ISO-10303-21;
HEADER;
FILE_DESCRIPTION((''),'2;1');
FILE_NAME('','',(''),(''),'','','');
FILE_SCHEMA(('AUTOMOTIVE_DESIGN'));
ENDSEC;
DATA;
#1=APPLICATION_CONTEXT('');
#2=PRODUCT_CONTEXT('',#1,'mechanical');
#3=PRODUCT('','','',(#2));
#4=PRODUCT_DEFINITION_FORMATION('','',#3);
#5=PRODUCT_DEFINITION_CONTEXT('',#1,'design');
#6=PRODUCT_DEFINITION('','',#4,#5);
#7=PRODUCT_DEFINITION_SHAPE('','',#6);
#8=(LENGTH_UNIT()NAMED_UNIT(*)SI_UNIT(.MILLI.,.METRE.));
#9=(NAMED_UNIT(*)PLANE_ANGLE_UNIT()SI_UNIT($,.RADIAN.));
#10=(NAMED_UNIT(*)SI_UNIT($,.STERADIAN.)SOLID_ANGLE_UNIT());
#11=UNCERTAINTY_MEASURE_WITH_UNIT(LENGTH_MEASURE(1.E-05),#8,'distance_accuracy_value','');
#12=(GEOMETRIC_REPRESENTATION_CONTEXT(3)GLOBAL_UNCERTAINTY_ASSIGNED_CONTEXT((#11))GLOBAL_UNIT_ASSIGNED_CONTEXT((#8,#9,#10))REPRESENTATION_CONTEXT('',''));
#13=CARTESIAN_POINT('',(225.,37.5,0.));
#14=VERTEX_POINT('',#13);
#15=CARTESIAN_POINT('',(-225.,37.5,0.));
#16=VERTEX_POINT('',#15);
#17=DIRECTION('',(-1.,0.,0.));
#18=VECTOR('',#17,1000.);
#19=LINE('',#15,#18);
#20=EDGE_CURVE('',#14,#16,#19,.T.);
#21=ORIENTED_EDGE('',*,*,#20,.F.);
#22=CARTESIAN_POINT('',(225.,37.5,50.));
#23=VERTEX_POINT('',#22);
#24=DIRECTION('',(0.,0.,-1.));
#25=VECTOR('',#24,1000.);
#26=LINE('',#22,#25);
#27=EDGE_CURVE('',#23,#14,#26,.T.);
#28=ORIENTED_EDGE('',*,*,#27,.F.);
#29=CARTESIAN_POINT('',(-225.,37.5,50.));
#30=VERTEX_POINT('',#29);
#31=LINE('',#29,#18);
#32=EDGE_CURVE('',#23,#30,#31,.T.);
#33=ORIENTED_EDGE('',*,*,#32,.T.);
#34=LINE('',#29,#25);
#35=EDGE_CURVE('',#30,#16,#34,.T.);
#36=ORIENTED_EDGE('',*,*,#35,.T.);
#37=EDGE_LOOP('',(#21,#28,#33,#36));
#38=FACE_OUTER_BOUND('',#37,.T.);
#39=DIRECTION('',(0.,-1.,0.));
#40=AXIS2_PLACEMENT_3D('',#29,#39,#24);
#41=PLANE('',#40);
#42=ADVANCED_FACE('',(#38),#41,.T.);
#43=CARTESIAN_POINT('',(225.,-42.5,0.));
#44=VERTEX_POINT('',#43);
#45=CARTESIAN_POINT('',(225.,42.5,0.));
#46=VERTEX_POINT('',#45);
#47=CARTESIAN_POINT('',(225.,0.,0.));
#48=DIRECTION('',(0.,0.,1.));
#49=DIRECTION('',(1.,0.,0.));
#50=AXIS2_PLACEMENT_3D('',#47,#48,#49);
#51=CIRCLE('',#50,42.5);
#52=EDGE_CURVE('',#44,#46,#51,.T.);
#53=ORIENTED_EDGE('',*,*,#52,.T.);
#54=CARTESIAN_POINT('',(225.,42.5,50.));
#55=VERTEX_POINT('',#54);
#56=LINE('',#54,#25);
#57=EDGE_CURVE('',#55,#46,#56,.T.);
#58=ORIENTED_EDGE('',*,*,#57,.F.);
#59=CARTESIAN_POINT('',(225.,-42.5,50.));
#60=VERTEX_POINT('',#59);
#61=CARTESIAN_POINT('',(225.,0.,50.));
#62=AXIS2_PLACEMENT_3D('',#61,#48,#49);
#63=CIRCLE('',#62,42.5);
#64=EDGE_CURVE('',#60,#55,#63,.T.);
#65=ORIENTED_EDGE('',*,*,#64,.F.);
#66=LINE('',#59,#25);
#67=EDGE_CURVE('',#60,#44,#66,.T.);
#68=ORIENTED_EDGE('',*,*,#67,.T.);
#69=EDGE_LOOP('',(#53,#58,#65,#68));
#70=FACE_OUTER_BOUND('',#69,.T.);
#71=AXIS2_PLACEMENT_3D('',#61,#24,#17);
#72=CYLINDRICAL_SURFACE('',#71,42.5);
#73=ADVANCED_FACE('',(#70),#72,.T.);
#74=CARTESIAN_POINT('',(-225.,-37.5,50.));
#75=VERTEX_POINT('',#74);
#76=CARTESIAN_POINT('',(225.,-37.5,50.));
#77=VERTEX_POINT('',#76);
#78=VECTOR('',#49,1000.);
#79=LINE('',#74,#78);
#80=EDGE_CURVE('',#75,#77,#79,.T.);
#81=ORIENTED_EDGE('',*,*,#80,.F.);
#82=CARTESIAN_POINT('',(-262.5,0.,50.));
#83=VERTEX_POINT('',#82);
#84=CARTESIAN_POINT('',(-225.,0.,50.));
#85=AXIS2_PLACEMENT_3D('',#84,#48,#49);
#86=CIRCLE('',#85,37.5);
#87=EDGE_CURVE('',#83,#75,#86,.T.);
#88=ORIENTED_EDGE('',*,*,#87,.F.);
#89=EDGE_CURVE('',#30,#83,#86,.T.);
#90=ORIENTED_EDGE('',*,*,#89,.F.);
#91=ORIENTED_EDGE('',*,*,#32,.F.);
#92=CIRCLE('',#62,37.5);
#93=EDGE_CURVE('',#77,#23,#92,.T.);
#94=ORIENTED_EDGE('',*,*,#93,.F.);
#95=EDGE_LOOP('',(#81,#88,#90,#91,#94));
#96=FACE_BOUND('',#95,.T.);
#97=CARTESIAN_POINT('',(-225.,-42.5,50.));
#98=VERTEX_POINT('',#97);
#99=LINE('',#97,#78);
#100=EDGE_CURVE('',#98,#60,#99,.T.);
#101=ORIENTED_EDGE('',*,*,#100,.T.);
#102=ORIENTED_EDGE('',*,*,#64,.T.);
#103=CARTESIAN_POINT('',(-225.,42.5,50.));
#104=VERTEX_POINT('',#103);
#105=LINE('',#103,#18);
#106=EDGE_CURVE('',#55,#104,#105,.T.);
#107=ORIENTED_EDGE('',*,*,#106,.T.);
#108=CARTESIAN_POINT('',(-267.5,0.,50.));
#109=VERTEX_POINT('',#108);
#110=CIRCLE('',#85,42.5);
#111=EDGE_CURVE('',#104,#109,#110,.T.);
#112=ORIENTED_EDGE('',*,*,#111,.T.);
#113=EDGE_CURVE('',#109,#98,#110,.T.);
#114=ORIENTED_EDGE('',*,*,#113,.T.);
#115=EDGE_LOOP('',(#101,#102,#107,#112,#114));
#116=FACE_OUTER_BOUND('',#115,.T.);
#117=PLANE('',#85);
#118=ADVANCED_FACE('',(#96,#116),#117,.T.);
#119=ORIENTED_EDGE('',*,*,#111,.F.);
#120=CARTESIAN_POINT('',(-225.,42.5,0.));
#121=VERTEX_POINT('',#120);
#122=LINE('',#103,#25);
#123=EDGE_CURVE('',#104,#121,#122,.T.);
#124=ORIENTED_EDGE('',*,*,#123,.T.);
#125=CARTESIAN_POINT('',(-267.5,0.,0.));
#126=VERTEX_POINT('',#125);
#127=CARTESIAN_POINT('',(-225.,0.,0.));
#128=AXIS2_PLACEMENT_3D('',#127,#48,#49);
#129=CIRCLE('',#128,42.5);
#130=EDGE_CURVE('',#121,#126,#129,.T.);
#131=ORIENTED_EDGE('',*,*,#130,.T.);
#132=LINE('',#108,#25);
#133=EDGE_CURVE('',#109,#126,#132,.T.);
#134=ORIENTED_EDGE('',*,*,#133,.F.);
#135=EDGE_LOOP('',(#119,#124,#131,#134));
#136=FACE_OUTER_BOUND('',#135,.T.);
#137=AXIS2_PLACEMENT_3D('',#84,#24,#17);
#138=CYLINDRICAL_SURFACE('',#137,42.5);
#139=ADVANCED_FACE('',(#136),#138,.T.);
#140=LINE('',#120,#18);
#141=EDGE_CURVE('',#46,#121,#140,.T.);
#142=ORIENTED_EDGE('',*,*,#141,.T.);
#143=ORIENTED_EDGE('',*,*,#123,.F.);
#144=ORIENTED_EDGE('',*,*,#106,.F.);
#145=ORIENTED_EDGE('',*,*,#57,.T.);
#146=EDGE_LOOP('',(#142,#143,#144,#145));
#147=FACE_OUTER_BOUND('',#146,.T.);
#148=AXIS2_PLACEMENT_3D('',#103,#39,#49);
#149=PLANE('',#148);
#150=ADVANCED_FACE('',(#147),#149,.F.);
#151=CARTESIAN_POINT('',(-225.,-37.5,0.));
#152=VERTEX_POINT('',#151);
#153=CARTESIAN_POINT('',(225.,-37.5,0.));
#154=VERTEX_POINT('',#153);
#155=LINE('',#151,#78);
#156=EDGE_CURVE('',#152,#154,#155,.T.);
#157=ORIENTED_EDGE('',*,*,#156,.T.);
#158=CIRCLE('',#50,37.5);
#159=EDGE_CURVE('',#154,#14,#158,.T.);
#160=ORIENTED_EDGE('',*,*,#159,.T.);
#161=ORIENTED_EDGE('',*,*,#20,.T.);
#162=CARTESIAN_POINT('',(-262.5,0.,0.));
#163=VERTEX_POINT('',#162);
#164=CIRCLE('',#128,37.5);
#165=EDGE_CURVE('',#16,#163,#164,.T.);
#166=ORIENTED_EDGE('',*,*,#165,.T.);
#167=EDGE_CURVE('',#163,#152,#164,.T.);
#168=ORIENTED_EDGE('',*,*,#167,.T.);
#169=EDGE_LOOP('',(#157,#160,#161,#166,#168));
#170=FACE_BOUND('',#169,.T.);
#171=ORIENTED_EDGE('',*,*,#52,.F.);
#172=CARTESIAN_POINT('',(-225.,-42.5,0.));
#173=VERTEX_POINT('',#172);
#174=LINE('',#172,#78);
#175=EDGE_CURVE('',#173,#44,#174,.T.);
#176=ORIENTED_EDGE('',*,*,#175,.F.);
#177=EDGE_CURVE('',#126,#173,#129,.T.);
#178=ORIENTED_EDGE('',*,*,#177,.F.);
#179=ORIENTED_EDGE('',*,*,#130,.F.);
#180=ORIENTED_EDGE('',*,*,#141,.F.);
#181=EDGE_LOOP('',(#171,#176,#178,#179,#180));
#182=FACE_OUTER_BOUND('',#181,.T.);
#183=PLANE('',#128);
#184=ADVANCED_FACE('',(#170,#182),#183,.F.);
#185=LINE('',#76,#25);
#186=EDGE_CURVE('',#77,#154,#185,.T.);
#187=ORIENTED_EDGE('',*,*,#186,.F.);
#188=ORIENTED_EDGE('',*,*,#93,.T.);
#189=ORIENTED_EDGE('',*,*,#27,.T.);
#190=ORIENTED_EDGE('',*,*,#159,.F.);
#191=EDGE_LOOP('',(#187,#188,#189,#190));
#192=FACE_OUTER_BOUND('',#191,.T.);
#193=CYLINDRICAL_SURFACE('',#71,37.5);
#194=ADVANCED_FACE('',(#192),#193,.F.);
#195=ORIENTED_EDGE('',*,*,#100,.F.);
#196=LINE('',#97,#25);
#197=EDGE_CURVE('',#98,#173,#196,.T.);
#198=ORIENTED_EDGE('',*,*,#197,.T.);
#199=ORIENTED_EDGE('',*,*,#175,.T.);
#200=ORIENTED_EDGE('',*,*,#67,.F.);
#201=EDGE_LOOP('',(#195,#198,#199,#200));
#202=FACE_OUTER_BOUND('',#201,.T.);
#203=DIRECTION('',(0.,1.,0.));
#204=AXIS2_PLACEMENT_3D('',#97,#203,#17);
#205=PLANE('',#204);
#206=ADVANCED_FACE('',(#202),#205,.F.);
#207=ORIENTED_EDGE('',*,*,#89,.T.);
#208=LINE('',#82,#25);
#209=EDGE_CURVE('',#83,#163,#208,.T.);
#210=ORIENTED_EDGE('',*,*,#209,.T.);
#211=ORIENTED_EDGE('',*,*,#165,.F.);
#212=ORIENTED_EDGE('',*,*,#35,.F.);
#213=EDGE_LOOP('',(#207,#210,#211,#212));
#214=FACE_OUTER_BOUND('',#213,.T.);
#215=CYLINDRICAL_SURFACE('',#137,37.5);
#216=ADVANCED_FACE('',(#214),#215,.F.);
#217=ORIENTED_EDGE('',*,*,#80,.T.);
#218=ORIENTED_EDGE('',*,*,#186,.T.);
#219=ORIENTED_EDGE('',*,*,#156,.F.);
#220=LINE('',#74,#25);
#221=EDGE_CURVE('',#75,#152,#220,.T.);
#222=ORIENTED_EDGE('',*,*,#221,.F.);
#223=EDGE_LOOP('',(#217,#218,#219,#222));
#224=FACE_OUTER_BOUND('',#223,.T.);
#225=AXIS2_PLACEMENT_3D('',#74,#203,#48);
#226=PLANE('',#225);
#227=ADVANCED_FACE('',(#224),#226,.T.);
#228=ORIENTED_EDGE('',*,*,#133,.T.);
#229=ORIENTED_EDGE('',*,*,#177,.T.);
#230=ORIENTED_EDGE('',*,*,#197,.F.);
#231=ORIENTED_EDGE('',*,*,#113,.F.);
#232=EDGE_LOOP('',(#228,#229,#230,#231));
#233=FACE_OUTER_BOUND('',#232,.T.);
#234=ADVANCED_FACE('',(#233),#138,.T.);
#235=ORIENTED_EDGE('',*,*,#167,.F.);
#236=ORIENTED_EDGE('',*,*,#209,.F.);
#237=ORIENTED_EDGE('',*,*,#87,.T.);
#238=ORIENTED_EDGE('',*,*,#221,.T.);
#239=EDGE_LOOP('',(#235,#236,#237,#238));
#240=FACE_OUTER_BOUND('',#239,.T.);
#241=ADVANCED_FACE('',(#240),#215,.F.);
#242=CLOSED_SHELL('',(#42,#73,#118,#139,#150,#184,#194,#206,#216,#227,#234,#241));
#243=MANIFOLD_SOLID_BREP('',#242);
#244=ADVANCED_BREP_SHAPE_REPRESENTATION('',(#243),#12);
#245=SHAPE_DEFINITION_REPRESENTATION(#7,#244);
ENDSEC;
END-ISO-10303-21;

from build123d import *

# Parameters (mm, degrees)
EXTRUDE_1_DEPTH = 50


with BuildPart() as part:
    # 草图1 → 凸台-拉伸1 (new body)
    with BuildSketch(Plane.XY):
        with BuildLine():
            Line((-225, 42.5), (225, 42.5))
            ThreePointArc((225, 42.5), (267.5, 0), (225, -42.5))
            Line((225, -42.5), (-225, -42.5))
            ThreePointArc((-225, -42.5), (-267.5, 0), (-225, 42.5))
        make_face()
        with BuildLine():
            Line((-225, 37.5), (225, 37.5))
            ThreePointArc((225, 37.5), (262.5, 0), (225, -37.5))
            Line((225, -37.5), (-225, -37.5))
            ThreePointArc((-225, -37.5), (-262.5, 0), (-225, 37.5))
        make_face(mode=Mode.SUBTRACT)
    extrude(amount=EXTRUDE_1_DEPTH)


solid = part.part
